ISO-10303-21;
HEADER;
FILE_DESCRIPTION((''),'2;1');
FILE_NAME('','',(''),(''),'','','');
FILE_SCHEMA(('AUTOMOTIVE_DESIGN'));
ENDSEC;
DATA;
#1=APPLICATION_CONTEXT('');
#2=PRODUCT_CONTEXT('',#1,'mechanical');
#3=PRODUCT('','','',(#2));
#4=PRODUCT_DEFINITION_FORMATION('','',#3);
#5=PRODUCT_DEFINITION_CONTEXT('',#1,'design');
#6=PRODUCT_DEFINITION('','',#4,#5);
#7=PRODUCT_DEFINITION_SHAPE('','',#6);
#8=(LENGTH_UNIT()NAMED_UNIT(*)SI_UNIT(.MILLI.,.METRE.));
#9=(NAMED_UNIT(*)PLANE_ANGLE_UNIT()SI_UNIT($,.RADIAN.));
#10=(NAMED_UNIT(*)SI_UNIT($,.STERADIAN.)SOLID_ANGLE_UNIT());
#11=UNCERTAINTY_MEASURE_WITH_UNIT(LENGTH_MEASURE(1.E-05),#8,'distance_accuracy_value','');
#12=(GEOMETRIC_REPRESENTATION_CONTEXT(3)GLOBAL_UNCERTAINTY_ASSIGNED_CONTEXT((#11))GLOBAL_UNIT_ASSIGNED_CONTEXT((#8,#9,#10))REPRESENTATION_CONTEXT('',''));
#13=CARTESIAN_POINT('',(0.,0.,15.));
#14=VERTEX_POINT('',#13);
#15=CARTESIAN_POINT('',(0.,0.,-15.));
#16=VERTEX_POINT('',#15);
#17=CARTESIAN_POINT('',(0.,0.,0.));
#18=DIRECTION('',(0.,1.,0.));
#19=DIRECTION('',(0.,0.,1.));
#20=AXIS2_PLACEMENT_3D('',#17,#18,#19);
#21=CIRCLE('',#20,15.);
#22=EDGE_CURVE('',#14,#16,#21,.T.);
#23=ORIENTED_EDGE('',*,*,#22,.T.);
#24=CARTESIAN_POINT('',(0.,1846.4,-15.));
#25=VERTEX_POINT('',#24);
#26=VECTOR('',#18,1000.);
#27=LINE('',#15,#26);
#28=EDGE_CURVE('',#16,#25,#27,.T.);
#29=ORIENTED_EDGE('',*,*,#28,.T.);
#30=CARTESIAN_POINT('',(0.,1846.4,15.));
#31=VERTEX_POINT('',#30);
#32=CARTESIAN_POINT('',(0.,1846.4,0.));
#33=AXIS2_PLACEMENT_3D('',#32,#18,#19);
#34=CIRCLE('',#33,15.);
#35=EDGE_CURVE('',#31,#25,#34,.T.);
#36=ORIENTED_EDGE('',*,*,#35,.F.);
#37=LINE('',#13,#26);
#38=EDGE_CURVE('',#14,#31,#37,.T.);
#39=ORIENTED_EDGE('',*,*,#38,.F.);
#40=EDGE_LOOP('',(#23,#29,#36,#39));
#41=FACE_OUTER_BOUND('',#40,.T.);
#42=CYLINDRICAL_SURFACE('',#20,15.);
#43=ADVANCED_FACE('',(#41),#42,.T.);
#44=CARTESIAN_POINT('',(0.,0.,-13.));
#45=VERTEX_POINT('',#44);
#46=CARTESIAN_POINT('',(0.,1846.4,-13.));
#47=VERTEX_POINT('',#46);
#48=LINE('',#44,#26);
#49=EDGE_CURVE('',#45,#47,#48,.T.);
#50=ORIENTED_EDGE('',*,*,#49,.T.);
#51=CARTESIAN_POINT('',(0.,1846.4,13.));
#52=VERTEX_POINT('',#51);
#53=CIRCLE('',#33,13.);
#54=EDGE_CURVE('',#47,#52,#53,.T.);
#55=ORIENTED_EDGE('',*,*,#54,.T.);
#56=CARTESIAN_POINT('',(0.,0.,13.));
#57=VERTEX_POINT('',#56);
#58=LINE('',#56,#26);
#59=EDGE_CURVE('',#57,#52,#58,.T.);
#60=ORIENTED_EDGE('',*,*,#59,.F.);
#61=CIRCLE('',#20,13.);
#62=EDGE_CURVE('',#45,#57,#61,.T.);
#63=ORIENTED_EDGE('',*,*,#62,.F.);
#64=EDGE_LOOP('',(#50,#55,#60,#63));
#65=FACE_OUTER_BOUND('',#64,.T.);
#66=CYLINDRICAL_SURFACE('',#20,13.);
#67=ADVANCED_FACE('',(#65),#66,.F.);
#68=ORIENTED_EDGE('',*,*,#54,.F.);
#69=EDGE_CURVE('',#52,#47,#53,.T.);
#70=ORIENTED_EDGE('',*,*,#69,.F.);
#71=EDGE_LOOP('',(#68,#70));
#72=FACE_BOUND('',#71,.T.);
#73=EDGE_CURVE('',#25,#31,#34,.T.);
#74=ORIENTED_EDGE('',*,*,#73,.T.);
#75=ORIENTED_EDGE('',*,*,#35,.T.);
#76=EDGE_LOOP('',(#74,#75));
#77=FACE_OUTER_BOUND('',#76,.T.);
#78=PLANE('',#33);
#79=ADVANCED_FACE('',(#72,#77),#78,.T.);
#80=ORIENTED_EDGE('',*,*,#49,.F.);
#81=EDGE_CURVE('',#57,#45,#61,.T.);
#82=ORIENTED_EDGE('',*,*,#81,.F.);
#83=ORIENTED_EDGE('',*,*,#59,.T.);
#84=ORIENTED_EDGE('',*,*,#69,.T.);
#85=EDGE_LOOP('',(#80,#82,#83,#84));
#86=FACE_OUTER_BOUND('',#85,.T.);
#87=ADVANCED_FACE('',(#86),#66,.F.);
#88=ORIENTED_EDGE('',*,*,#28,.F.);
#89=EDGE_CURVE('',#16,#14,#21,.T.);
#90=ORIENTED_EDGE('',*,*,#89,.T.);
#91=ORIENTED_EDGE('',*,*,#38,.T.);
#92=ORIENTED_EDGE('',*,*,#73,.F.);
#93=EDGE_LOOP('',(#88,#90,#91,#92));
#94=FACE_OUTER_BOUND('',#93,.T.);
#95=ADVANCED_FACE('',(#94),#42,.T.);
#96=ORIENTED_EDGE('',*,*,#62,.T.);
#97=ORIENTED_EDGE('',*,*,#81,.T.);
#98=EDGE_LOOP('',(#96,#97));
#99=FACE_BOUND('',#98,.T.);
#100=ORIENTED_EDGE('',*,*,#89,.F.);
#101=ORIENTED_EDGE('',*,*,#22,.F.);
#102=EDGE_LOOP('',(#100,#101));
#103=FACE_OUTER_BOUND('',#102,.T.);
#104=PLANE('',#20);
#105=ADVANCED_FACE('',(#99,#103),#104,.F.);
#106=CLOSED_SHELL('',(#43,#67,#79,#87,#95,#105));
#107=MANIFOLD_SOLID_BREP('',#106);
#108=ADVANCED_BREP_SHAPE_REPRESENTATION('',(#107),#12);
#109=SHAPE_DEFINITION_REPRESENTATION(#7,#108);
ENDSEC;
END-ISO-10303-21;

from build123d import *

# Parameters (mm, degrees)
SWEEP_THIN1_PROFILE_R   = 15
SWEEP_THIN1_PROFILE_R_2 = 13


with BuildPart() as part:
    # Sweep-Thin1: sweep along a path in Sketch1
    with BuildLine(Plane.XY) as sweep_thin1_path:
        Line((0, 0), (0, 1846.4))
    # Sweep-Thin1 profile (on start of the path) → Sweep-Thin1 (sweep)
    with BuildSketch(Plane.ZX):
        Circle(SWEEP_THIN1_PROFILE_R)
        Circle(SWEEP_THIN1_PROFILE_R_2, mode=Mode.SUBTRACT)
    sweep(path=sweep_thin1_path.line)


solid = part.part
